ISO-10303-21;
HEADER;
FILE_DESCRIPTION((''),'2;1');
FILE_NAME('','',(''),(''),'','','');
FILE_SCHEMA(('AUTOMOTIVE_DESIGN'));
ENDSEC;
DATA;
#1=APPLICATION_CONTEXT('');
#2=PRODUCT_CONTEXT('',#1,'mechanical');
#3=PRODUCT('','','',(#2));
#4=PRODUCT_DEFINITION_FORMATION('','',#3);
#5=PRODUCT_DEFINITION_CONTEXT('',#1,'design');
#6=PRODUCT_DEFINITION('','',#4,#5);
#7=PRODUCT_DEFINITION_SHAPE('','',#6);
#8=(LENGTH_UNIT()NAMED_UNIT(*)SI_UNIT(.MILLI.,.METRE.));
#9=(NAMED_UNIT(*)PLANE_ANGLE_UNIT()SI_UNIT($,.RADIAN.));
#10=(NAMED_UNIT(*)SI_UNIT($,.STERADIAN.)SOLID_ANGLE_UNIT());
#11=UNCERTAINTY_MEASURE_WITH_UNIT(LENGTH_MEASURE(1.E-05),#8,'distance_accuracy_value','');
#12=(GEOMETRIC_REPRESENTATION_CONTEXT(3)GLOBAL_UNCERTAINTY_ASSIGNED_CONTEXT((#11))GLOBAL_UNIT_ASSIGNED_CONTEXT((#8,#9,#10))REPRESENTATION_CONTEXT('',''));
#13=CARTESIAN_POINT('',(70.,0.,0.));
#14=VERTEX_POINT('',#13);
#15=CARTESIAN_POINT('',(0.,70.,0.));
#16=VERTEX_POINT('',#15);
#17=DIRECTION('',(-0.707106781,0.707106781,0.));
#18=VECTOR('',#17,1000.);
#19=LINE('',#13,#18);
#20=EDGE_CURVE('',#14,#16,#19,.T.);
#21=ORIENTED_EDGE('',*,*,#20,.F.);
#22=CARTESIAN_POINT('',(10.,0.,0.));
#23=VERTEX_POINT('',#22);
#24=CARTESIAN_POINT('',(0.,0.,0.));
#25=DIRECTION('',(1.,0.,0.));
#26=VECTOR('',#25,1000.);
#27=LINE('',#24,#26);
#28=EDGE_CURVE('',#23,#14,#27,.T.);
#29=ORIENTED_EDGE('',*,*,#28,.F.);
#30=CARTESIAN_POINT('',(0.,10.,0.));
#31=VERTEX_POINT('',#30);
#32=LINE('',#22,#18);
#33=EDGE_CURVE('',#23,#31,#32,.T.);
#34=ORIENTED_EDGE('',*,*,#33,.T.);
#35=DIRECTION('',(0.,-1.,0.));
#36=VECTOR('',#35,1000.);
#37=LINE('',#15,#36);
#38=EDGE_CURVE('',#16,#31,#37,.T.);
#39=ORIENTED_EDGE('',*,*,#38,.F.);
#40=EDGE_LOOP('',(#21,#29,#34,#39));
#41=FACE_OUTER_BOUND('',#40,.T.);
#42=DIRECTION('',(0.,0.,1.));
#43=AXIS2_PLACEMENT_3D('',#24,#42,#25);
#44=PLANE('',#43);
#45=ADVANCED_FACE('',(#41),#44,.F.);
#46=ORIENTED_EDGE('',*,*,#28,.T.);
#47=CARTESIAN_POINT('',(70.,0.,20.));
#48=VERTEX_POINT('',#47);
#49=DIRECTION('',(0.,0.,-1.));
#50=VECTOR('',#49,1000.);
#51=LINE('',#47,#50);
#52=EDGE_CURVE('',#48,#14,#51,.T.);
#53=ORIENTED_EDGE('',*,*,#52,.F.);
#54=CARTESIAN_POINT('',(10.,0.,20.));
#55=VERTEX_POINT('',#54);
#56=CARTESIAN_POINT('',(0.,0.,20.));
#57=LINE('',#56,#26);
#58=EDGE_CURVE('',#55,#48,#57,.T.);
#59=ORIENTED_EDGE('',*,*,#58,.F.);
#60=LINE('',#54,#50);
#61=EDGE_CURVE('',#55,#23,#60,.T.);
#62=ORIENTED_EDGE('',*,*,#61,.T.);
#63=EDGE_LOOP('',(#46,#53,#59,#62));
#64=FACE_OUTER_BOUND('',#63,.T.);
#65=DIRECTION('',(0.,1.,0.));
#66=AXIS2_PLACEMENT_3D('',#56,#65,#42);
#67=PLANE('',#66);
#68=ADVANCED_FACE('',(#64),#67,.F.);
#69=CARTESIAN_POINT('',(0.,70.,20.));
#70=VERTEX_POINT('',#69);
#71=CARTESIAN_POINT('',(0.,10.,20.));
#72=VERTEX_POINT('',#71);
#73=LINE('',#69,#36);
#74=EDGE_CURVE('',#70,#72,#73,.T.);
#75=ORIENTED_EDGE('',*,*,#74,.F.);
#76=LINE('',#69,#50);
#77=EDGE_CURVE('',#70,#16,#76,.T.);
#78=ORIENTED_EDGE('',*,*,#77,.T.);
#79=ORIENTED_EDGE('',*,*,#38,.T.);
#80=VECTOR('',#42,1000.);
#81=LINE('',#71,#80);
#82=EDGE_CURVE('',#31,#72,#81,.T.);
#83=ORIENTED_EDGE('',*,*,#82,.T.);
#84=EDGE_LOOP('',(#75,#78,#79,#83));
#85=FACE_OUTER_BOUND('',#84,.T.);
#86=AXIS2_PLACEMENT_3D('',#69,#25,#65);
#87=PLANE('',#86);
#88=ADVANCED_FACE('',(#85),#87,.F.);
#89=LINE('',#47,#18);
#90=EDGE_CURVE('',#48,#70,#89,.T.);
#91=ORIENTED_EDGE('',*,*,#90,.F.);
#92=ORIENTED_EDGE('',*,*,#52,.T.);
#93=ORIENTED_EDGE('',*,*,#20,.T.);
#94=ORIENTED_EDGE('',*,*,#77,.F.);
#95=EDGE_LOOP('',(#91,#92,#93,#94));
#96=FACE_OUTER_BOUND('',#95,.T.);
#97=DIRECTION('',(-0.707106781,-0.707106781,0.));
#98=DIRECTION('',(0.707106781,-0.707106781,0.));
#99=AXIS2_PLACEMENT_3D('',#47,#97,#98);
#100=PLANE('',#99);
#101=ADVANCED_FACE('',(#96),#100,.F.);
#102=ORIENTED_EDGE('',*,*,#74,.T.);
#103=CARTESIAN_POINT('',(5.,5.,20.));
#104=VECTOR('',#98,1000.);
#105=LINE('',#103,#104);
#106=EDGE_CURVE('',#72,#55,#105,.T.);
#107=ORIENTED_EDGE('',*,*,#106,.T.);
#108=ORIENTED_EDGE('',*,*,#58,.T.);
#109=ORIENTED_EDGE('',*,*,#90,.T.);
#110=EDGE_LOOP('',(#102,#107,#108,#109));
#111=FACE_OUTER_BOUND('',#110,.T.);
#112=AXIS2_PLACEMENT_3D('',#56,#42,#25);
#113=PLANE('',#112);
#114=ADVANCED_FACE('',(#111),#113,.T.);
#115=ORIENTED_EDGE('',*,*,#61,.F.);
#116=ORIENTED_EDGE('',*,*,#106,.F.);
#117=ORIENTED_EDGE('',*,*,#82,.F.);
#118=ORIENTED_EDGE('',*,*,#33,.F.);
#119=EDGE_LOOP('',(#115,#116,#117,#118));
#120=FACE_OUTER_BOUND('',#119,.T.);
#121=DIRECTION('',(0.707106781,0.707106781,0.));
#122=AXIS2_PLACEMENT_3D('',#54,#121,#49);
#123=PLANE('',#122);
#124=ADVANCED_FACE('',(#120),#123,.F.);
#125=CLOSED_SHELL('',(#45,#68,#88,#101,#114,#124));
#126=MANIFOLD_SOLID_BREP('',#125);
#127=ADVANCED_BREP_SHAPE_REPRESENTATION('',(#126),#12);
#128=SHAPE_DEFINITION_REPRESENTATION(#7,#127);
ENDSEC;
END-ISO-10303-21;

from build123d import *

# Parameters (mm, degrees)
EXTRUDE_1_DEPTH = 20
CHAMFER_1_SIZE  = 10


with BuildPart() as part:
    # 草图1 → 凸台-拉伸1 (new body)
    with BuildSketch(Plane.XY):
        Polygon((0, 70), (0, 0), (70, 0), align=None)
    extrude(amount=EXTRUDE_1_DEPTH)

    # 倒角1
    chamfer_1_edges = [part.edges().sort_by_distance(p)[0] for p in [
        (0, 0, 10),
    ]]
    chamfer(chamfer_1_edges, length=CHAMFER_1_SIZE)


solid = part.part
